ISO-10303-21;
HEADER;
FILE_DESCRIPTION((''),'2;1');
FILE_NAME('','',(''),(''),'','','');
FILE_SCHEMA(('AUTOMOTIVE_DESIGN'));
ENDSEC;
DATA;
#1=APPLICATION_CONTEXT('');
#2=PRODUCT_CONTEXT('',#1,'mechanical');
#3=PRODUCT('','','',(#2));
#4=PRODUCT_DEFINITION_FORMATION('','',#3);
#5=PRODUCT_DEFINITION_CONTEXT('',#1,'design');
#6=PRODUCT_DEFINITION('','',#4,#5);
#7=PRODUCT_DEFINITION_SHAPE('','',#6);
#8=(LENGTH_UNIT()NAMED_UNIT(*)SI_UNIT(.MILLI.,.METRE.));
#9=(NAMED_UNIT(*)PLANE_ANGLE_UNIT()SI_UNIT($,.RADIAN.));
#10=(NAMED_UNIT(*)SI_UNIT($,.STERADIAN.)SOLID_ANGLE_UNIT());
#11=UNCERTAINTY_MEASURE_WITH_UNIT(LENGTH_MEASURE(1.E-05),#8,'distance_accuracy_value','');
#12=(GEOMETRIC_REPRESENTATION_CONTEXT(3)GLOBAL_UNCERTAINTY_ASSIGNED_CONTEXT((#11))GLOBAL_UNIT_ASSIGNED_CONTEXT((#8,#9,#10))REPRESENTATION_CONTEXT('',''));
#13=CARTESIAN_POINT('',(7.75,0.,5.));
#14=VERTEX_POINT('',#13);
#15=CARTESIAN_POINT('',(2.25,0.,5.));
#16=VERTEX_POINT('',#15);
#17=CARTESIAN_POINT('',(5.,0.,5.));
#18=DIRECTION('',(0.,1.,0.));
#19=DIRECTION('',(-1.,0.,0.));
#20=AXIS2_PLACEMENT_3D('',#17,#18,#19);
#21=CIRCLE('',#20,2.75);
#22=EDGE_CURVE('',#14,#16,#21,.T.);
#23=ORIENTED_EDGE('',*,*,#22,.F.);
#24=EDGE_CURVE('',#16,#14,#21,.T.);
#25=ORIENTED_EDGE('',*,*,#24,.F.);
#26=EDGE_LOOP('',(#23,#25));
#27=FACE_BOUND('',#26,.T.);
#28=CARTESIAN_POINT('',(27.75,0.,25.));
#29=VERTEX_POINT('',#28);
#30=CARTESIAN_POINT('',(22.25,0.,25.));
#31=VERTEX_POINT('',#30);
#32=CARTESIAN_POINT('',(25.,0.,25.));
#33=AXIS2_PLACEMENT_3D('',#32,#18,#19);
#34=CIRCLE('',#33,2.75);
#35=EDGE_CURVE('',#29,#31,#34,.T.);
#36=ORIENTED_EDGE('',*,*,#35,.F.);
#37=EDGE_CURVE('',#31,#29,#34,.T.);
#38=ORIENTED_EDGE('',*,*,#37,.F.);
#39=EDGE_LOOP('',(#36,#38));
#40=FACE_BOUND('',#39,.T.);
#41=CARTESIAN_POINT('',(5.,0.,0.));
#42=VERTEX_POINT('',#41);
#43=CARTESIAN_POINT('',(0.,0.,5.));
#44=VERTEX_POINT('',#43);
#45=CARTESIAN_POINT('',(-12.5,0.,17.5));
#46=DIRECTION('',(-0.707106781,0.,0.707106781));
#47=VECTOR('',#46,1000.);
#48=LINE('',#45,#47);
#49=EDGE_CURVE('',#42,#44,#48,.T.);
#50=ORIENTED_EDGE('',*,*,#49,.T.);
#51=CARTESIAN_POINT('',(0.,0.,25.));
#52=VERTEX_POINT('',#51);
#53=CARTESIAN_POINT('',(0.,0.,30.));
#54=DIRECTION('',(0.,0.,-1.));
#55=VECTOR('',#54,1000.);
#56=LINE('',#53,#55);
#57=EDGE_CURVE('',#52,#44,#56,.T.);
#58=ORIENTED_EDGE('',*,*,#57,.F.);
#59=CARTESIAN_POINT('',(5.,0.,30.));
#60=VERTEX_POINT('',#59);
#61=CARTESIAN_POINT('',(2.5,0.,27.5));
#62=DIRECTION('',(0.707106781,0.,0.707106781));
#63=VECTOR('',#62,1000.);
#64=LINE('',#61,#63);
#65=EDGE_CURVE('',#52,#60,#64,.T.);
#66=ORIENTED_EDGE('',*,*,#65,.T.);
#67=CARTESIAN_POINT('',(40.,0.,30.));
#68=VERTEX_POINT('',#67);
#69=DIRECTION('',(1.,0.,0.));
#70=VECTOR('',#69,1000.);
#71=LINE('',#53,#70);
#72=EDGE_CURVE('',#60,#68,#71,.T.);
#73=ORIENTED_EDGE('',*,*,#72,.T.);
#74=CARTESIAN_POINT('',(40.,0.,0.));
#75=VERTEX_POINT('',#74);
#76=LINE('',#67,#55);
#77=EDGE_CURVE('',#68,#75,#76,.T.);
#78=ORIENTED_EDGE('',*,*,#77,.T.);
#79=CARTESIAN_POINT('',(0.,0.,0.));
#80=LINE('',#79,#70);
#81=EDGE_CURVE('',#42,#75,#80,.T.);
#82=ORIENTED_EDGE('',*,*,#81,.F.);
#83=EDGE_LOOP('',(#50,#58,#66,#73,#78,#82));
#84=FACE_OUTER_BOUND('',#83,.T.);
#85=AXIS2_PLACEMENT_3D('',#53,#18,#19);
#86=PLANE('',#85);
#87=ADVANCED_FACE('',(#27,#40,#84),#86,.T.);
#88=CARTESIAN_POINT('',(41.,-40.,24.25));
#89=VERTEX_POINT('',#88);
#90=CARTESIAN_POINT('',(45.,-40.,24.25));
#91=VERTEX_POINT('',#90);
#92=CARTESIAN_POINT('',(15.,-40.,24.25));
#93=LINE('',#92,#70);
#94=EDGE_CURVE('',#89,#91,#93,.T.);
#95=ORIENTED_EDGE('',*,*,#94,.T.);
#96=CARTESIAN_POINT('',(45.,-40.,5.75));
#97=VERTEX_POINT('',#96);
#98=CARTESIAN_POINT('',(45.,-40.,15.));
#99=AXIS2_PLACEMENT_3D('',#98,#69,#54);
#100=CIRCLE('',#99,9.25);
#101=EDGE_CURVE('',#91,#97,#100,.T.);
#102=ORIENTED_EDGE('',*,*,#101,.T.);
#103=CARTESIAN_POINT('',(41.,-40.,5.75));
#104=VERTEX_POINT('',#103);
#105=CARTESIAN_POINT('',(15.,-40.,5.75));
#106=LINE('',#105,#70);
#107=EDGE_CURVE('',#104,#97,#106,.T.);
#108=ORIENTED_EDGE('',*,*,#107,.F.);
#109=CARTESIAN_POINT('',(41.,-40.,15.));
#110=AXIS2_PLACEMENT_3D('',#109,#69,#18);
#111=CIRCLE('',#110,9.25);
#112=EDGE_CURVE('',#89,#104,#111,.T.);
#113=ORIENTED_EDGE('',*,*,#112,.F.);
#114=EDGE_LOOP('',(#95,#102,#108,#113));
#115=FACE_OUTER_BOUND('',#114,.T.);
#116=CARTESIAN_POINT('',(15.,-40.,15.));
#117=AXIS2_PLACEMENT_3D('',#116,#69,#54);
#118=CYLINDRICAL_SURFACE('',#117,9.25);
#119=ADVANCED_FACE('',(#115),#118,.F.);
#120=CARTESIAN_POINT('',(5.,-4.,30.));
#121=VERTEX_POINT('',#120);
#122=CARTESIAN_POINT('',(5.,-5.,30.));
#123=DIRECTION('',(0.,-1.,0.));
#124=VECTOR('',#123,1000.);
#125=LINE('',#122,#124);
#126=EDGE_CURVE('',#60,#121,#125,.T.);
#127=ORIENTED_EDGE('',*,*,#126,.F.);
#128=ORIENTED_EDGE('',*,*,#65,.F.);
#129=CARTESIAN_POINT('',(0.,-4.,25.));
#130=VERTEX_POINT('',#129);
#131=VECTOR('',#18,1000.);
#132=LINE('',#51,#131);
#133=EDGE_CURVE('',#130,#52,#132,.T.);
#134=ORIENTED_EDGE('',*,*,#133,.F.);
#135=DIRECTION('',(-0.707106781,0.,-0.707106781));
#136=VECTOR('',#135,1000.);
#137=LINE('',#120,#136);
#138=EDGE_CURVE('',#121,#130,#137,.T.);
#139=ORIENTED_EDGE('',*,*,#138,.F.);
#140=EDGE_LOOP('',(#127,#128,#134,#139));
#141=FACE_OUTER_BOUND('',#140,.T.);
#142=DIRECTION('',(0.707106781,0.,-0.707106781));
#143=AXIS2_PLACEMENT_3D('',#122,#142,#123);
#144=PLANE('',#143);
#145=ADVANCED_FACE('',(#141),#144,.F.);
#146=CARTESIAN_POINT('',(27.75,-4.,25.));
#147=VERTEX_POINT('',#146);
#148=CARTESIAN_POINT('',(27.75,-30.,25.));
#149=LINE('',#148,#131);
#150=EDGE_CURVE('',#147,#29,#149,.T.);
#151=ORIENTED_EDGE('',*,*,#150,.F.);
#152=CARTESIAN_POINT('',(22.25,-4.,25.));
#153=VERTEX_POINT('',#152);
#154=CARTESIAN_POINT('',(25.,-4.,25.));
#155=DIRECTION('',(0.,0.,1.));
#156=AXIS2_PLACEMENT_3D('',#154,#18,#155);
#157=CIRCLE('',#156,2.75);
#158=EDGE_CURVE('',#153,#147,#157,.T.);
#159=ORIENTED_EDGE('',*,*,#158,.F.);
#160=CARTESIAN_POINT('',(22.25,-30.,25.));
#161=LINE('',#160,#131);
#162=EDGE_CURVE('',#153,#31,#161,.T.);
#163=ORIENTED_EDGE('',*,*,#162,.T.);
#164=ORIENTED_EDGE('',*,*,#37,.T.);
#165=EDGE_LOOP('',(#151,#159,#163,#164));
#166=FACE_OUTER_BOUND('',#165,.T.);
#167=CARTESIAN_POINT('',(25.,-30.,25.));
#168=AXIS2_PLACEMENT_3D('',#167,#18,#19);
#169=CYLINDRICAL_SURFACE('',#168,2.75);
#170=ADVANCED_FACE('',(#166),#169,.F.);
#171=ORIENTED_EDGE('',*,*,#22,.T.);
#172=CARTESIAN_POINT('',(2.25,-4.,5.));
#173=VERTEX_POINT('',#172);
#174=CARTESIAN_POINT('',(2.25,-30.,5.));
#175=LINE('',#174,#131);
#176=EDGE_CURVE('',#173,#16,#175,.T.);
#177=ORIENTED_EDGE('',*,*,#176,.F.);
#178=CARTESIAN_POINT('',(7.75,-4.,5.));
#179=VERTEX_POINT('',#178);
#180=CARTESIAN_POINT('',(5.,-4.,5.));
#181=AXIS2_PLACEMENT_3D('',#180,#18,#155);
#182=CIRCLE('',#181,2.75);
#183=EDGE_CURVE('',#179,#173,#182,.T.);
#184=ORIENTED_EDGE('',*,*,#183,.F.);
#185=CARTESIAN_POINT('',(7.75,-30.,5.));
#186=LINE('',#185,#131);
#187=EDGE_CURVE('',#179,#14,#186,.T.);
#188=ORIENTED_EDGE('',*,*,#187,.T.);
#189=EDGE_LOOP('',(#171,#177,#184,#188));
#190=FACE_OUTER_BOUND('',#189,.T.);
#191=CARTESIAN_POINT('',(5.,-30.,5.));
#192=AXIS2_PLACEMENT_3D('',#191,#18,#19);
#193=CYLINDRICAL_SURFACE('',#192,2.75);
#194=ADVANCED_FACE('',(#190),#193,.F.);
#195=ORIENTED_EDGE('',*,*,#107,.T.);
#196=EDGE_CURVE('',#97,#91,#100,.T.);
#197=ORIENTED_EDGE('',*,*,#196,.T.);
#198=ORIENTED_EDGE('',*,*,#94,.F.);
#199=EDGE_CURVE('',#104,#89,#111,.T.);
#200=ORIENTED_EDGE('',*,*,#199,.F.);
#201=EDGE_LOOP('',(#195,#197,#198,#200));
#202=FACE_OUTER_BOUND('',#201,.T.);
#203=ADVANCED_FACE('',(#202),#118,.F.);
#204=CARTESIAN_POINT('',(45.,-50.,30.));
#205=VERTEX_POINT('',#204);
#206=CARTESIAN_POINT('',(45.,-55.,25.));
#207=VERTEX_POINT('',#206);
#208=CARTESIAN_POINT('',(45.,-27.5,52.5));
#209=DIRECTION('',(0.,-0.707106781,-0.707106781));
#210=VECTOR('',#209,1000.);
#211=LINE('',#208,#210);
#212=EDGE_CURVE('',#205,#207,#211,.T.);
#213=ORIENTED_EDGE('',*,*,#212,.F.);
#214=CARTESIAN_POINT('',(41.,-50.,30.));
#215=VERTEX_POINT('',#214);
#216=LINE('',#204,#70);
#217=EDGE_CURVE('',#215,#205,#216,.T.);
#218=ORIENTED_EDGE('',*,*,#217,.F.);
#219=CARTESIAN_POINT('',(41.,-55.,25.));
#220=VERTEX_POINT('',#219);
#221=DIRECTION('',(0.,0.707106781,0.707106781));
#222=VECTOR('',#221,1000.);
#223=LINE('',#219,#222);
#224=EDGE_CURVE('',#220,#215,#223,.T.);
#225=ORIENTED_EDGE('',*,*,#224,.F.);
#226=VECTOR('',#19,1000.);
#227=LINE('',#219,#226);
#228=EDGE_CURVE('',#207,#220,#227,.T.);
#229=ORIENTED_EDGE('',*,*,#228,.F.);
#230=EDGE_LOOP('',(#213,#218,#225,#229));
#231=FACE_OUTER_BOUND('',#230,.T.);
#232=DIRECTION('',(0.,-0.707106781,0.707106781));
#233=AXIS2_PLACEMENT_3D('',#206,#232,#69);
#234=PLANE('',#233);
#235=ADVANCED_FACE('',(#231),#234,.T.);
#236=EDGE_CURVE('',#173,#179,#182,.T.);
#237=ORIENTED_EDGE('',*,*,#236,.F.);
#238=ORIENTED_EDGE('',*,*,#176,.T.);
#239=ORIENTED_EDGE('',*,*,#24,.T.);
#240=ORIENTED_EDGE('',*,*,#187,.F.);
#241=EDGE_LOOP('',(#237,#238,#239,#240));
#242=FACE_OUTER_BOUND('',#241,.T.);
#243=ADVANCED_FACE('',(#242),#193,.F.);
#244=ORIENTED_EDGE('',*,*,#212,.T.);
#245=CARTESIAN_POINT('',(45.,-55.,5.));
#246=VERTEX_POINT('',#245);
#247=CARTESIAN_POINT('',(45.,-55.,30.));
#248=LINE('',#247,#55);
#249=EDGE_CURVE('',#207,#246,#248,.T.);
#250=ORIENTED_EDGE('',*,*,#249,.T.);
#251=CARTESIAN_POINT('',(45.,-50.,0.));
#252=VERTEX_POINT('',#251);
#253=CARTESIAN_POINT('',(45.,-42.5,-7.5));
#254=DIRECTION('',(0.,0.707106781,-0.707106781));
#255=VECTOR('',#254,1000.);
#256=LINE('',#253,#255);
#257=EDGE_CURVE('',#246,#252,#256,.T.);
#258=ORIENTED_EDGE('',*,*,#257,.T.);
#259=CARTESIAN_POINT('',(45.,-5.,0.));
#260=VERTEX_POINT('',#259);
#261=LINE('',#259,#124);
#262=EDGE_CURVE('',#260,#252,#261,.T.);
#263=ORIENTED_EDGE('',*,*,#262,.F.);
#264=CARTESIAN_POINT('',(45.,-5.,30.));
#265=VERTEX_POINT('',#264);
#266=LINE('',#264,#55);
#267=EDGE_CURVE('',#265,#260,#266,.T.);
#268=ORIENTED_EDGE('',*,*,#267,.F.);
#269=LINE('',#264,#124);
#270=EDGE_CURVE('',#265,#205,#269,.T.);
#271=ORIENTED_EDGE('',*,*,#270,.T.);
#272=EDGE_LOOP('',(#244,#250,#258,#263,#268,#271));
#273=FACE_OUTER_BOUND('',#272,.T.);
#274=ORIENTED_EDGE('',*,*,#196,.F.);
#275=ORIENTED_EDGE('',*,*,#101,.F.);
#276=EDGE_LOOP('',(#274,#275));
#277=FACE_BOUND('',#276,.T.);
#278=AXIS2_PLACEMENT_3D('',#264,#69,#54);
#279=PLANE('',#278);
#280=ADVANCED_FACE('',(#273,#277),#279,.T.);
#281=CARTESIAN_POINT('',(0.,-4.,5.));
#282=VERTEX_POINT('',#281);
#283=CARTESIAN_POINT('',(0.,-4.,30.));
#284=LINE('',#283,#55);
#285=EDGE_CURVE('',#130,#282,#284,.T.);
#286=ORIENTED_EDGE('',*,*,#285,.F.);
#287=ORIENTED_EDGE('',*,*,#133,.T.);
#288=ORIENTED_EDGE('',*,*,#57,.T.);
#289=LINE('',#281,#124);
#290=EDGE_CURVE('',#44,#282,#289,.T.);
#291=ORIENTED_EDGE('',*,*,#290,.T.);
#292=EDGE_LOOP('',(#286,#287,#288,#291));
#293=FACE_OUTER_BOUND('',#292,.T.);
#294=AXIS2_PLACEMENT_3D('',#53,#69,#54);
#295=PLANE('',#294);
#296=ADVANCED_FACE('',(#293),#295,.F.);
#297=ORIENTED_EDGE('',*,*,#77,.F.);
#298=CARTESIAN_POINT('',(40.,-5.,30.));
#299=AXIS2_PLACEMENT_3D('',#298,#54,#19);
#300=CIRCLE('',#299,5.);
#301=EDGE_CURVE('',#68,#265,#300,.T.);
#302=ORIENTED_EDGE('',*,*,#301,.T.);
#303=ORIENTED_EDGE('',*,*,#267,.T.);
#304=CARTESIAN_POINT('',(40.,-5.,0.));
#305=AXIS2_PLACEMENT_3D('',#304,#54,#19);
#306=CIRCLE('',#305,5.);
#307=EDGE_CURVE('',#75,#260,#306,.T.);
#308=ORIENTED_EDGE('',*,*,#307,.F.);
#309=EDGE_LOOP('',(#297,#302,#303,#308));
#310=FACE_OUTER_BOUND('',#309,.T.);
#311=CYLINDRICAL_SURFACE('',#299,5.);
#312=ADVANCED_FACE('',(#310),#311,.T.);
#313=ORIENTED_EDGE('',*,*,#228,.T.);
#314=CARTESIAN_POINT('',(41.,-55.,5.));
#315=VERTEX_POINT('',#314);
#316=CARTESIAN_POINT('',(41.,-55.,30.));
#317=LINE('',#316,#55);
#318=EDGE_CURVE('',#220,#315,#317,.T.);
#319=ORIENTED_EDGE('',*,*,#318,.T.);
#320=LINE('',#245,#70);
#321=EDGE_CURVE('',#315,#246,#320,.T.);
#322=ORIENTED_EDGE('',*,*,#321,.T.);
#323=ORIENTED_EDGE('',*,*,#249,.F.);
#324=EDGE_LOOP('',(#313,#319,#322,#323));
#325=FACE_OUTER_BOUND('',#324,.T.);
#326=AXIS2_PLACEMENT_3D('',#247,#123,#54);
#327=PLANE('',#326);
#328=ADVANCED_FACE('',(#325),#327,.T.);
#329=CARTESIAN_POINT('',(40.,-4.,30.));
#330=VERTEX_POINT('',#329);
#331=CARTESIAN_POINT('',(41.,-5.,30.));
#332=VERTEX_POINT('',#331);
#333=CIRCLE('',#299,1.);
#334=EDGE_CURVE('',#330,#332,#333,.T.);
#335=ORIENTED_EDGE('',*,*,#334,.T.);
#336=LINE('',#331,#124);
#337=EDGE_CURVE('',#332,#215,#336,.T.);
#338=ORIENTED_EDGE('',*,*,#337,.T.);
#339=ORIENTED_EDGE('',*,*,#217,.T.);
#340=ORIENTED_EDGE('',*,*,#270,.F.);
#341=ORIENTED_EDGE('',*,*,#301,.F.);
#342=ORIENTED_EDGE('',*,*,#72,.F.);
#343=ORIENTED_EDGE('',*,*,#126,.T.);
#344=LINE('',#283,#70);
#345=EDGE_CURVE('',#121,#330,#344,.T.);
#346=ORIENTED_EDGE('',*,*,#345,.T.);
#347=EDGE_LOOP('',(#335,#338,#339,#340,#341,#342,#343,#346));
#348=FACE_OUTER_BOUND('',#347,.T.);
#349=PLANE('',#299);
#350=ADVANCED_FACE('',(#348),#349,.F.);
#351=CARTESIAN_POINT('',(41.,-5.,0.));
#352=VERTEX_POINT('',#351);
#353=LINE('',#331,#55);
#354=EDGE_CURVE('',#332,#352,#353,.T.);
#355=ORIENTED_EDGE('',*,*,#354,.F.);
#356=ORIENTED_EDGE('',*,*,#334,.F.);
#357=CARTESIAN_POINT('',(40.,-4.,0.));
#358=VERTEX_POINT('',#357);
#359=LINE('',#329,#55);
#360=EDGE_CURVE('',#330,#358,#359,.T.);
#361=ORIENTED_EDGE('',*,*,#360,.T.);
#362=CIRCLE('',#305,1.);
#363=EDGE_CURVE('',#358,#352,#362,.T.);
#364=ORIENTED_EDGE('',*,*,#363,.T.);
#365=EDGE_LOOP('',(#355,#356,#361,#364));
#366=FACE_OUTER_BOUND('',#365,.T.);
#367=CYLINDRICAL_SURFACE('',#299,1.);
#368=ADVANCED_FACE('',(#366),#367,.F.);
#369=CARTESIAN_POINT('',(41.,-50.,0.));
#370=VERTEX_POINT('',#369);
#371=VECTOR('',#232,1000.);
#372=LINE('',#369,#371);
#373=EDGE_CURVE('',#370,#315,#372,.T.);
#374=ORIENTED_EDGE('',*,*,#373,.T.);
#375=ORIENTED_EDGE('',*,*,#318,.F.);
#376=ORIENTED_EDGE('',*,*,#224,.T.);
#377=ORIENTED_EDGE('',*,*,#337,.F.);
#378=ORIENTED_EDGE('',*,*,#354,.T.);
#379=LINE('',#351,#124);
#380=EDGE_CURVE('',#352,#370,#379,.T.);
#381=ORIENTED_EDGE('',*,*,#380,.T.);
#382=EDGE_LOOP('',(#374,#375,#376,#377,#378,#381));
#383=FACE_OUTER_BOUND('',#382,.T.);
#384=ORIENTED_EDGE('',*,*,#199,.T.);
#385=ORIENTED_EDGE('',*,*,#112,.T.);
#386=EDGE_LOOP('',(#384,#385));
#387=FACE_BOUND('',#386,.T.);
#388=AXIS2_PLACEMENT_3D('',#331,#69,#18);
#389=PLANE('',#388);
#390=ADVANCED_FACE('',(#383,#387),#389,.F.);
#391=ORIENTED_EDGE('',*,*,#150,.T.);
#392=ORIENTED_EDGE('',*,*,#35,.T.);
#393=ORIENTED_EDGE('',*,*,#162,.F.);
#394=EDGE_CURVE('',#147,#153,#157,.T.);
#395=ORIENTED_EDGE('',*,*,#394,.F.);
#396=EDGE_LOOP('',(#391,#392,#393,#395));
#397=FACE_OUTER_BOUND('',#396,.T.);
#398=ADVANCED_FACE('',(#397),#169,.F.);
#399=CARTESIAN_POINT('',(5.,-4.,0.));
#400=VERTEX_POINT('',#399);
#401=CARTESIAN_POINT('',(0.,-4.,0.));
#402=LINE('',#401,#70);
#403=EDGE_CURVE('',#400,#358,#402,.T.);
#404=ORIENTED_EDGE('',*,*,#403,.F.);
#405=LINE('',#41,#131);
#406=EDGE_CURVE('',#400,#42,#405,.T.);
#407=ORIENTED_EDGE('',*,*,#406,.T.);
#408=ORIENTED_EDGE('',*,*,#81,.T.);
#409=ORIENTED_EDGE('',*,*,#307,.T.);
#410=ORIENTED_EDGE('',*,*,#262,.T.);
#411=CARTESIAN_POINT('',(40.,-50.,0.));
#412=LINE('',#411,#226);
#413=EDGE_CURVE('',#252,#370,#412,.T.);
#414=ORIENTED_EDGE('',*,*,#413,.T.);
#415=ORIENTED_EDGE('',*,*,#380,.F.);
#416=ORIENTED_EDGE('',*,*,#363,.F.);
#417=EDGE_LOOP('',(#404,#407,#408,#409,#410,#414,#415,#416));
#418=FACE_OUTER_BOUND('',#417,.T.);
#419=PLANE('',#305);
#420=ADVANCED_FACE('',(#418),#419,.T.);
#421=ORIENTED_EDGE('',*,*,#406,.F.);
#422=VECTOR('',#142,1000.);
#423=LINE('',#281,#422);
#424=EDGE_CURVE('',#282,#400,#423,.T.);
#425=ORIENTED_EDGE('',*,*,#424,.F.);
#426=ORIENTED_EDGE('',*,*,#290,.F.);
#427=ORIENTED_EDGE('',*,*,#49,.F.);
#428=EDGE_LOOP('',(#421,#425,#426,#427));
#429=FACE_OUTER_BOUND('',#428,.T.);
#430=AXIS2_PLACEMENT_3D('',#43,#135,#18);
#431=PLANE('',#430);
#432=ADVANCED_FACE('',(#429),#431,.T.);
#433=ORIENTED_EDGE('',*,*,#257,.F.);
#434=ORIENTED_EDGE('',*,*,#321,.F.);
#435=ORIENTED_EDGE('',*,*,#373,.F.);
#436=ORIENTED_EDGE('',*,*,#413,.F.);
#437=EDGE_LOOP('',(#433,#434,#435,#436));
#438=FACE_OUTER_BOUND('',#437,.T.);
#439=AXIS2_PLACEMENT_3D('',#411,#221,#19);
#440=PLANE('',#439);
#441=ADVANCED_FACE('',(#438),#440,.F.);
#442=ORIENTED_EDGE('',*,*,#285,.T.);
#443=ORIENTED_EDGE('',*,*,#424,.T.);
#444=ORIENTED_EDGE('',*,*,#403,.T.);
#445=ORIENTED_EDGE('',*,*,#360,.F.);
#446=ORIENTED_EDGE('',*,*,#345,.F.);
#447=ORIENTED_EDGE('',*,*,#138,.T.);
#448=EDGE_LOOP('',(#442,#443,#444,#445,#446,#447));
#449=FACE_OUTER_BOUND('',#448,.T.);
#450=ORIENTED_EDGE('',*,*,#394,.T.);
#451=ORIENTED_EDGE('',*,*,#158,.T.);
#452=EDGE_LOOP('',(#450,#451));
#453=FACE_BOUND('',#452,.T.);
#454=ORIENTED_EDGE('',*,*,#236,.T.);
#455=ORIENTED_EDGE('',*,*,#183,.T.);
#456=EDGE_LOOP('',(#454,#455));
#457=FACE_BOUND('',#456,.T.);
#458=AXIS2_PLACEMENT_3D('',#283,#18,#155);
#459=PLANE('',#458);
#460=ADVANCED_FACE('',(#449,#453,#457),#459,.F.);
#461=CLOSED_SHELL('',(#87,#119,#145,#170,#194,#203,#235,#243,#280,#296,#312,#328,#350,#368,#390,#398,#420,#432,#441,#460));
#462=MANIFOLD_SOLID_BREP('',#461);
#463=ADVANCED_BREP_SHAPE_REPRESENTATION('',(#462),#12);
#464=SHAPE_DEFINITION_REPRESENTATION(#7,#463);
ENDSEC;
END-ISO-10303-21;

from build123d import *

# Parameters (mm, degrees)
EXTRUDE_1_DEPTH     = 30
SKETCH_3_R          = 9.25
CUT_EXTRUDE_1_DEPTH = 30
SKETCH_4_R          = 2.75
CUT_EXTRUDE_2_DEPTH = 30
CHAMFER_1_SIZE      = 5


with BuildPart() as part:
    # 草图1 → 凸台-拉伸1 (new body)
    with BuildSketch(Plane.XY):
        with BuildLine():
            Line((0, 0), (40, 0))
            ThreePointArc((40, 0), (43.535533906, -1.464466094), (45, -5))
            Line((45, -5), (45, -55))
            Line((45, -55), (41, -55))
            Line((41, -55), (41, -5))
            ThreePointArc((41, -5), (40.707106781, -4.292893219), (40, -4))
            Line((40, -4), (0, -4))
            Line((0, -4), (0, 0))
        make_face()
    extrude(amount=EXTRUDE_1_DEPTH)

    # 草图3 → 切除-拉伸1 (cut)
    with BuildSketch(Plane(origin=(45, 0, 0), x_dir=(0, 0, -1), z_dir=(1, 0, 0))):
        with Locations((-15, -40)):
            Circle(SKETCH_3_R)
    extrude(amount=-CUT_EXTRUDE_1_DEPTH, mode=Mode.SUBTRACT)

    # 草图4 → 切除-拉伸2 (cut)
    with BuildSketch(Plane(origin=(0, 0, 0), x_dir=(1, 0, 0), z_dir=(0, 1, 0))):
        with Locations(Location((5, -5, 0), (0, 0, 180))):
            Circle(SKETCH_4_R)
        with Locations(Location((25, -25, 0), (0, 0, 180))):
            Circle(SKETCH_4_R)
    extrude(amount=-CUT_EXTRUDE_2_DEPTH, mode=Mode.SUBTRACT)

    # 倒角1
    chamfer_1_edges = [part.edges().sort_by_distance(p)[0] for p in [
        (43, -55, 0),
        (0, -2, 30),
        (43, -55, 30),
        (0, -2, 0),
    ]]
    chamfer(chamfer_1_edges, length=CHAMFER_1_SIZE)


solid = part.part
